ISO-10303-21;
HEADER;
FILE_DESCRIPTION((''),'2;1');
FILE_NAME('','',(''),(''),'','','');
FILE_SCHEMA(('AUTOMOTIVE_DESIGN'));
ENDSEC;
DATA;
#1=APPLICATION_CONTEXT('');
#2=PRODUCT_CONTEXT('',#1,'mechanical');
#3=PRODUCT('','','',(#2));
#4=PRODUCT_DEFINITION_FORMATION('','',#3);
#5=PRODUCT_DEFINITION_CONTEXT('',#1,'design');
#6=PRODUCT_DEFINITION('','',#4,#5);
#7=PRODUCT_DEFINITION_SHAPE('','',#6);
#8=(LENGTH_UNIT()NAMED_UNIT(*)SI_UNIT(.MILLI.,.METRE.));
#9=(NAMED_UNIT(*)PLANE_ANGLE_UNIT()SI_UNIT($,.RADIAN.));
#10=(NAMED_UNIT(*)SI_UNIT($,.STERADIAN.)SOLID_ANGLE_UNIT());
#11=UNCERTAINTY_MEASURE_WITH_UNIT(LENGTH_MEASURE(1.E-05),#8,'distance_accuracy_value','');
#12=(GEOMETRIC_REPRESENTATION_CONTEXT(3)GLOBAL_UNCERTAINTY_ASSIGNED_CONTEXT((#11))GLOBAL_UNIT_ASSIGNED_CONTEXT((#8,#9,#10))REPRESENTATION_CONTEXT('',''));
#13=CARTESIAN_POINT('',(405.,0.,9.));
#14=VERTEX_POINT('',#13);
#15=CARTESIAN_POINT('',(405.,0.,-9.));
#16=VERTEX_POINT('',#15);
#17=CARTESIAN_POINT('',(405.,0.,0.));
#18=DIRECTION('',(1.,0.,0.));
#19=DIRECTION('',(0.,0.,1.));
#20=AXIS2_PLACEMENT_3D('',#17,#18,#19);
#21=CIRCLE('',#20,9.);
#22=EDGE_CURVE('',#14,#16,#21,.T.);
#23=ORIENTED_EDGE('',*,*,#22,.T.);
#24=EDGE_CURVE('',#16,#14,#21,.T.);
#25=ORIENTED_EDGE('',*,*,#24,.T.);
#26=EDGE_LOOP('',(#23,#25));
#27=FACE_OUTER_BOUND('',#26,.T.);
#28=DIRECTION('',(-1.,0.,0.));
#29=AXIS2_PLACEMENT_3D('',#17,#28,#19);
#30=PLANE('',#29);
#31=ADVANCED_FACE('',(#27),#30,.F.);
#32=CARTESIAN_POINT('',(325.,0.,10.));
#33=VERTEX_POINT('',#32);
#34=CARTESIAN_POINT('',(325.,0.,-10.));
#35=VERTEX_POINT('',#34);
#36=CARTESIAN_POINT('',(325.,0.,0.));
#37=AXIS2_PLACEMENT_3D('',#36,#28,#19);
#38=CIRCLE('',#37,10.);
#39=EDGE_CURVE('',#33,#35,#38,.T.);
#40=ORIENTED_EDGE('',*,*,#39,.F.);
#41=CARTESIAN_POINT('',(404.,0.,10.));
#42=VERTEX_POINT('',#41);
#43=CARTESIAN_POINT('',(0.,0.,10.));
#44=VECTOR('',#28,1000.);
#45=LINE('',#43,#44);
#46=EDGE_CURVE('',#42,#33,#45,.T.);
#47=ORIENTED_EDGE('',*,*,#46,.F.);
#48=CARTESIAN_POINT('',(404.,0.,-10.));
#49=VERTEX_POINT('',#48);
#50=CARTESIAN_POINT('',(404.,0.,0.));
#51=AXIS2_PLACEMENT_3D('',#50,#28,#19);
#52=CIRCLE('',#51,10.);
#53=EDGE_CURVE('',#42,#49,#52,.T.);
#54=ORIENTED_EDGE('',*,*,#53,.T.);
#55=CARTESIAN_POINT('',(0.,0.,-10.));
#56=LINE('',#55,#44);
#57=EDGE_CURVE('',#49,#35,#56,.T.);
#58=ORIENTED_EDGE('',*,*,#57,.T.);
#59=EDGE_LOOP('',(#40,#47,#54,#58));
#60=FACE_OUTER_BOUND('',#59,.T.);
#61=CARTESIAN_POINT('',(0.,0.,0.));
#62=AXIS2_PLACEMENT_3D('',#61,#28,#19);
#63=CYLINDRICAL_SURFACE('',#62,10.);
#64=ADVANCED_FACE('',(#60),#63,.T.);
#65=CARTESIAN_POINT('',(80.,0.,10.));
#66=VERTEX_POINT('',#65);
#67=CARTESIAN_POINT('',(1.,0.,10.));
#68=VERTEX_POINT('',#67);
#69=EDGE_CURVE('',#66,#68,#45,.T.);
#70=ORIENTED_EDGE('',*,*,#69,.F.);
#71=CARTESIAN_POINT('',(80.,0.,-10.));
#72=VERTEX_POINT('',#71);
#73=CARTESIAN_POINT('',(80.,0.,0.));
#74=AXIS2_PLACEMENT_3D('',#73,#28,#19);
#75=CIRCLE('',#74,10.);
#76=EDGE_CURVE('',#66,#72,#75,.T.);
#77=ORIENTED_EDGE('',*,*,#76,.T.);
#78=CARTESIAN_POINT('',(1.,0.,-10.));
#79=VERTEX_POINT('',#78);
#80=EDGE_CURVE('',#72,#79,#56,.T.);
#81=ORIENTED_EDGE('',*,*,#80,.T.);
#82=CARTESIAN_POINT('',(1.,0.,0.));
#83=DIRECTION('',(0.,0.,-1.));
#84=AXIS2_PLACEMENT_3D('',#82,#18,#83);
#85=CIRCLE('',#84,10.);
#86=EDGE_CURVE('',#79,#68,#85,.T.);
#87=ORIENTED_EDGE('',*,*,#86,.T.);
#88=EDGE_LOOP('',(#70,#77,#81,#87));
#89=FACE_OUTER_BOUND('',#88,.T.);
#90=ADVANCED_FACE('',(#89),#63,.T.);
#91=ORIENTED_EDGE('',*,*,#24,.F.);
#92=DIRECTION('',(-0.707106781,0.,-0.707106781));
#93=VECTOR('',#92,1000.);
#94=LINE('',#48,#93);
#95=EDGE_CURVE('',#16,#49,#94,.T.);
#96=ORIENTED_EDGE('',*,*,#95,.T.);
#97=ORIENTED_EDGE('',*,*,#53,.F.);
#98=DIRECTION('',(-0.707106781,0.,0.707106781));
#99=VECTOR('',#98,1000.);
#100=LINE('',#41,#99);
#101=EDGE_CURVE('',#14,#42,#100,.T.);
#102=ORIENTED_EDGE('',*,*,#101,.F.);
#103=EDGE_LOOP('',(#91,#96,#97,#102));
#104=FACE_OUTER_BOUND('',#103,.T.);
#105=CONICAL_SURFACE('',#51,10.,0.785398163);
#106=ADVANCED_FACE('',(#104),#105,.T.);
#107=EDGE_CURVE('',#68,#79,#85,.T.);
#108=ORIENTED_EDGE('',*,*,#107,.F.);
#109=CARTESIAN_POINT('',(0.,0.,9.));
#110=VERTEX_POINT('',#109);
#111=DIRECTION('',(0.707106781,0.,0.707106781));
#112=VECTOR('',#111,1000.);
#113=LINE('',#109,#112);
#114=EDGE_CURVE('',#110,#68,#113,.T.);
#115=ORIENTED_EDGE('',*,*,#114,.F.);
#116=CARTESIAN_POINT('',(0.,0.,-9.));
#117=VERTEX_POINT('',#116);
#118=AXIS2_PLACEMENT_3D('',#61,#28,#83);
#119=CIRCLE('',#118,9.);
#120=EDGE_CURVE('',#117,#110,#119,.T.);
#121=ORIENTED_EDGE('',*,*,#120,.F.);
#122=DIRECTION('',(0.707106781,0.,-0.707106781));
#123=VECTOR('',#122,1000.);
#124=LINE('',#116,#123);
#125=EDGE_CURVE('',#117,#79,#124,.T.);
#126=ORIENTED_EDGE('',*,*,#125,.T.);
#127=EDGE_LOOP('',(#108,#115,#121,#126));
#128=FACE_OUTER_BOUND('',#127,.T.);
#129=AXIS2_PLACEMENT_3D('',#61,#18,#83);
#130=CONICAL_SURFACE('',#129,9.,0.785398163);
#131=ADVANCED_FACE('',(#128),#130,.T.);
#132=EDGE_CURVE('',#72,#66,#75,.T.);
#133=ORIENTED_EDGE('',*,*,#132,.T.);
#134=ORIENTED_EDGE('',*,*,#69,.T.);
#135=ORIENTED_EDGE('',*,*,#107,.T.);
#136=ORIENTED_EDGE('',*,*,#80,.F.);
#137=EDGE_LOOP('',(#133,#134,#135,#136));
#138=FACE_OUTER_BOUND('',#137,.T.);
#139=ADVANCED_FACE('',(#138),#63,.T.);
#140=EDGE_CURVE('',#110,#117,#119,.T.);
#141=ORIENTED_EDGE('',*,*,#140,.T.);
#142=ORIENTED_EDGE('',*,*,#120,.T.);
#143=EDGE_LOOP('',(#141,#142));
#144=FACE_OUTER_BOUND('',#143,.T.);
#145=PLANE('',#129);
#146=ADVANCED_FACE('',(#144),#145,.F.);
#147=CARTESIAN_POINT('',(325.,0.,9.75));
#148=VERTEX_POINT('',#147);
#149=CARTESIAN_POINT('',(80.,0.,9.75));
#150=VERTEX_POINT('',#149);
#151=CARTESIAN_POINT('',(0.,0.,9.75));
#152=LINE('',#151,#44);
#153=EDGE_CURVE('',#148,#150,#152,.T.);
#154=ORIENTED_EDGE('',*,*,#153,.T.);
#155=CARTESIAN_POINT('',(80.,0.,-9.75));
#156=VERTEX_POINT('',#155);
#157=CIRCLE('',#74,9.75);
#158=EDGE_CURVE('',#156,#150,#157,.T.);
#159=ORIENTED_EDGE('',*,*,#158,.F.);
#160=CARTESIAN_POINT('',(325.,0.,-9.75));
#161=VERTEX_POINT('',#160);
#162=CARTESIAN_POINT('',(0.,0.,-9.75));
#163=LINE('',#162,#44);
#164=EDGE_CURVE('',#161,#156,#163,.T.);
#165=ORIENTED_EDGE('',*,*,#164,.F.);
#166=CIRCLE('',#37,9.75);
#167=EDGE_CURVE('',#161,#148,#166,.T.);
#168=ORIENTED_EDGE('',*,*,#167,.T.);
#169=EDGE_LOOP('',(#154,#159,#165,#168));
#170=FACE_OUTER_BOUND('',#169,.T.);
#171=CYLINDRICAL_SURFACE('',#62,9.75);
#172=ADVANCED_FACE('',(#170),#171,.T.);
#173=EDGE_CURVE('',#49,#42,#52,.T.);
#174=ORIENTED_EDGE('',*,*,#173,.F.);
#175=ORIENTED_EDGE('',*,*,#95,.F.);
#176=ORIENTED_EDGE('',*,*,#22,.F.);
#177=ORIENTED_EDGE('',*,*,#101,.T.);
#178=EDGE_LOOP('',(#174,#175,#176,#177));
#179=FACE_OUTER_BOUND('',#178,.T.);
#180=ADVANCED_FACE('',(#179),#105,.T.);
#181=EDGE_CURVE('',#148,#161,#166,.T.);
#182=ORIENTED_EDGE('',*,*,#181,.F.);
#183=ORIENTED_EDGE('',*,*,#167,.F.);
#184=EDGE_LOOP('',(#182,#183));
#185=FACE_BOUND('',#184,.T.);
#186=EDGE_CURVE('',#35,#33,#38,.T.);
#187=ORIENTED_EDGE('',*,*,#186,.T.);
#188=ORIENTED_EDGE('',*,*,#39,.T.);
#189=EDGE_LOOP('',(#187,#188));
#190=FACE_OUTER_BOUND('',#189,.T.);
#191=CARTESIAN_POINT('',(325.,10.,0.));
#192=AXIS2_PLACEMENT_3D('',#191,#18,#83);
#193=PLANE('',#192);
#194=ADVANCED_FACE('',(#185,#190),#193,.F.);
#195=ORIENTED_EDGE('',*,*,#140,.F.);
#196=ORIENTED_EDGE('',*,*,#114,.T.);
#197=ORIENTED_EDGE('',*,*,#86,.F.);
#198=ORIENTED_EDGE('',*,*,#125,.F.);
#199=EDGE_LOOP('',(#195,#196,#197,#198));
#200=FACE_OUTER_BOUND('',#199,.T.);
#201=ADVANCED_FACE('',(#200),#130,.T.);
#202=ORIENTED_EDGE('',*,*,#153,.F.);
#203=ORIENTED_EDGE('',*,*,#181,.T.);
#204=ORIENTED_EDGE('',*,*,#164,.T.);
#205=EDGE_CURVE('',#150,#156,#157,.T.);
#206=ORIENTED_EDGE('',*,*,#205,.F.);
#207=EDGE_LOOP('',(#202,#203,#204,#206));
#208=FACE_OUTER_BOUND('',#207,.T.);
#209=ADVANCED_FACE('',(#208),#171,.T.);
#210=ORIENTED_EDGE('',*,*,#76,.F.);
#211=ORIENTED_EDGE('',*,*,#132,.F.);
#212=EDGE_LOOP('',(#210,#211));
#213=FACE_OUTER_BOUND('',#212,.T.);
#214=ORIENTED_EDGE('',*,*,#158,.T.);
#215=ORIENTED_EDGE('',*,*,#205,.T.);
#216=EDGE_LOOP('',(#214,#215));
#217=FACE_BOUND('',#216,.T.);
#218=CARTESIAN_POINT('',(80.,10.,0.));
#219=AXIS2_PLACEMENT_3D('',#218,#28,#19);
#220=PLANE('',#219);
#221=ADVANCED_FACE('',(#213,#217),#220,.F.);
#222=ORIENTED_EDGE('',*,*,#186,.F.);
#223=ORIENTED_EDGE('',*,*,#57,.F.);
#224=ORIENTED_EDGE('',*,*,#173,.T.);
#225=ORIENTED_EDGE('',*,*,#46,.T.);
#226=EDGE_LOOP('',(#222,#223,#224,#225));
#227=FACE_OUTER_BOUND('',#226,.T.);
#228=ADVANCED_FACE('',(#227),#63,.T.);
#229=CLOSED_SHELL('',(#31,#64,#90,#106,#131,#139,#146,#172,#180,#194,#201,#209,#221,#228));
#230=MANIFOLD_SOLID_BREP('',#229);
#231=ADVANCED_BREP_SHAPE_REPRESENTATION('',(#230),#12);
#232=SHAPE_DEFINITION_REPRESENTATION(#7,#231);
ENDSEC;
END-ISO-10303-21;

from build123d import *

# Parameters (mm, degrees)
CHAMFER1_SIZE = 1


with BuildPart() as part:
    # Sketch3 → Revolve1 (revolve)
    with BuildSketch(Plane.XY, mode=Mode.PRIVATE) as revolve1_sk:
        Polygon((325, 10), (405, 10), (405, 0), (0, 0), (0, 10), (80, 10), (80, 9.75), (325, 9.75), align=None)
    revolve(revolve1_sk.sketch.rotate(Axis((0, 0, 0), (1, 0, 0)), 90), axis=Axis((0, 0, 0), (1, 0, 0)))

    # Chamfer1
    chamfer1_edges = [part.edges().sort_by_distance(p)[0] for p in [
        (405, 0, -10),
        (0, 0, -10),
    ]]
    chamfer(chamfer1_edges, length=CHAMFER1_SIZE)


solid = part.part
